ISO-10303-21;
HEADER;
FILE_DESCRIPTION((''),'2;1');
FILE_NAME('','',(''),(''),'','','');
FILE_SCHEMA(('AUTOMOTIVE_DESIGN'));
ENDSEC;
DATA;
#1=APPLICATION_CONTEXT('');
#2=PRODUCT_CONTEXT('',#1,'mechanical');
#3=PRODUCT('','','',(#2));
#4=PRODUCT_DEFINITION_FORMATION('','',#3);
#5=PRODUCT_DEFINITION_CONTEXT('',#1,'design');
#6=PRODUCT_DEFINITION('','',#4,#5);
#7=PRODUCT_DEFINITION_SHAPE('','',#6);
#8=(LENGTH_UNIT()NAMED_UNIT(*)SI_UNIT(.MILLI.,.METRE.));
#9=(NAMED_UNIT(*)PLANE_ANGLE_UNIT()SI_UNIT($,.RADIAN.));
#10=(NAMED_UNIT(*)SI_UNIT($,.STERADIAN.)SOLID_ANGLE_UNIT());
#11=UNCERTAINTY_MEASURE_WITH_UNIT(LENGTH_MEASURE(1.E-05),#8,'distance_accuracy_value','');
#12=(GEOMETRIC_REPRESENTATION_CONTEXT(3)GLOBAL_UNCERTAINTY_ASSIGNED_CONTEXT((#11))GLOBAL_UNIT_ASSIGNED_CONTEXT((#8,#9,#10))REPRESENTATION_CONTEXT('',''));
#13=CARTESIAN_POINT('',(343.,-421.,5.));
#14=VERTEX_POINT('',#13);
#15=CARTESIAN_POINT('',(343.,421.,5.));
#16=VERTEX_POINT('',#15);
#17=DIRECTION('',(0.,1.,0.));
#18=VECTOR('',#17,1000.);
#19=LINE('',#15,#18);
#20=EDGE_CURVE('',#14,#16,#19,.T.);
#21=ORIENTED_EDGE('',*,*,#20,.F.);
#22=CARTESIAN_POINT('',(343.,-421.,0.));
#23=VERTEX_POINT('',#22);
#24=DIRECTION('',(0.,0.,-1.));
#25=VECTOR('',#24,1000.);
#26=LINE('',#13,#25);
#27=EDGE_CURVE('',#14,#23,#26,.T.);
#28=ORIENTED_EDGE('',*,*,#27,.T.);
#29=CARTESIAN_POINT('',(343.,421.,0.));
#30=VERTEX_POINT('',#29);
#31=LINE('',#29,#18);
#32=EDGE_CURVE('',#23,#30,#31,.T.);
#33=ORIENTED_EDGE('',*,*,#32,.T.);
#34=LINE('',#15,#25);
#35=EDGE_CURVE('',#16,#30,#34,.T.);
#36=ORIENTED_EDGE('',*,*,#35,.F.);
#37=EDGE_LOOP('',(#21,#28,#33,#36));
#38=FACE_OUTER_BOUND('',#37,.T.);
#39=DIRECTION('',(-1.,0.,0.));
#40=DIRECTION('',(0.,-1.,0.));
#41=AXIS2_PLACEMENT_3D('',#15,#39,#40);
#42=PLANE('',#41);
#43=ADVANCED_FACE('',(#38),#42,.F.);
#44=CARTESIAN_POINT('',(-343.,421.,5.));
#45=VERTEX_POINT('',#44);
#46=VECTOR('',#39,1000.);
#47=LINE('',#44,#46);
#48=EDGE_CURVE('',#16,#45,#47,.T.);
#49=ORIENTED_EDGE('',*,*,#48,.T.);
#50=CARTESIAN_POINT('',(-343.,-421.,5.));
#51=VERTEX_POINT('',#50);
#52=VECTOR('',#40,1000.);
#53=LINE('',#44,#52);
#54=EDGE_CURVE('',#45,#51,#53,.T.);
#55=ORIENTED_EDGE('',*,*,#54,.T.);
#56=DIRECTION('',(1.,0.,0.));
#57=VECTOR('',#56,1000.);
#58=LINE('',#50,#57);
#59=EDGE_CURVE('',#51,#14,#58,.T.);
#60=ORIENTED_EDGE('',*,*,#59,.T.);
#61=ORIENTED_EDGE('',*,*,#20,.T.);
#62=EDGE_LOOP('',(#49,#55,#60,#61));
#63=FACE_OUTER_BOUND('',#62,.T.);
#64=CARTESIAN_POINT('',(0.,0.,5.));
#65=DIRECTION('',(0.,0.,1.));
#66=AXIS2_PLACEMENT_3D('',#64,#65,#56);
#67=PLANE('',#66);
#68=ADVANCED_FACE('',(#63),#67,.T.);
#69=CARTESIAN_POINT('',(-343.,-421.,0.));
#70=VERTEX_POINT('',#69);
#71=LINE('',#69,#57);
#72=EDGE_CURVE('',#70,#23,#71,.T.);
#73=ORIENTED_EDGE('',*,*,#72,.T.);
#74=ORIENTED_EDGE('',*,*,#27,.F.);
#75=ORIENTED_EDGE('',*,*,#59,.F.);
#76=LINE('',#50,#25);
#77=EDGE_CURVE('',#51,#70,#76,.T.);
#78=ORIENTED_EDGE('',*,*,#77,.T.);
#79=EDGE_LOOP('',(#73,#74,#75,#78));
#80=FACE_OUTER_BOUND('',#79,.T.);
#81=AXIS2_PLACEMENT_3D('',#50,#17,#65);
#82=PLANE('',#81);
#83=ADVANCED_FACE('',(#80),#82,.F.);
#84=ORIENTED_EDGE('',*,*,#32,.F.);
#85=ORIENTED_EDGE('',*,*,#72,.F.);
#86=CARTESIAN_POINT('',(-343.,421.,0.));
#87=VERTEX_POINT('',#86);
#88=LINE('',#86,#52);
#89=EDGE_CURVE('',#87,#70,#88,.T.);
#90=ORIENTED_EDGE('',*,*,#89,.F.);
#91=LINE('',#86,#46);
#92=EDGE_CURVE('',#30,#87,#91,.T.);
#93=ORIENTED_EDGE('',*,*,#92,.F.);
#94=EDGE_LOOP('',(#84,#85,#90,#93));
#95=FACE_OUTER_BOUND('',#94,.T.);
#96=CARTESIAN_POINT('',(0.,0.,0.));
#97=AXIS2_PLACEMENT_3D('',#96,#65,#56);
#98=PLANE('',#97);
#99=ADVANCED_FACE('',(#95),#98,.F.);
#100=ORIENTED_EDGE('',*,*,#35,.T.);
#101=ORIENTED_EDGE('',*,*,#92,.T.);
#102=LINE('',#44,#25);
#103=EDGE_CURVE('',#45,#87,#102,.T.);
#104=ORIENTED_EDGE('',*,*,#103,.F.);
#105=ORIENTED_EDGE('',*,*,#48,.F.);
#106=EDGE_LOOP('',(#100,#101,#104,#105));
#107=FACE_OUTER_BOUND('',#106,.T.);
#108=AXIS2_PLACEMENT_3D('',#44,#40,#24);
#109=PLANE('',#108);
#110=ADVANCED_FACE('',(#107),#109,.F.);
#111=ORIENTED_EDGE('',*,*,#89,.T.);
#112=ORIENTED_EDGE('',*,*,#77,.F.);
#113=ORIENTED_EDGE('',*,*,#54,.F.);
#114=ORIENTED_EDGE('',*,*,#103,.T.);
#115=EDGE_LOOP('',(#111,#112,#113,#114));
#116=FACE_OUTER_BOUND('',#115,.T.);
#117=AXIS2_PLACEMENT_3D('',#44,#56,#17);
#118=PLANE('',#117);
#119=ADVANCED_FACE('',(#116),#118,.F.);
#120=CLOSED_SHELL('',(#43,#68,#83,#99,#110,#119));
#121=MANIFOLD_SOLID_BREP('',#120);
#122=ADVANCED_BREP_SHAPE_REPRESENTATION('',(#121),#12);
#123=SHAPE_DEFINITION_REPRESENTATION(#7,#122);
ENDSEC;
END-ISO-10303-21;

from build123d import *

# Parameters (mm, degrees)
SKETCH_1_W      = 686
SKETCH_1_H      = 842
EXTRUDE_1_DEPTH = 5


with BuildPart() as part:
    # 草图1 → 凸台-拉伸1 (new body)
    with BuildSketch(Plane.XY):
        Rectangle(SKETCH_1_W, SKETCH_1_H)
    extrude(amount=EXTRUDE_1_DEPTH)


solid = part.part
